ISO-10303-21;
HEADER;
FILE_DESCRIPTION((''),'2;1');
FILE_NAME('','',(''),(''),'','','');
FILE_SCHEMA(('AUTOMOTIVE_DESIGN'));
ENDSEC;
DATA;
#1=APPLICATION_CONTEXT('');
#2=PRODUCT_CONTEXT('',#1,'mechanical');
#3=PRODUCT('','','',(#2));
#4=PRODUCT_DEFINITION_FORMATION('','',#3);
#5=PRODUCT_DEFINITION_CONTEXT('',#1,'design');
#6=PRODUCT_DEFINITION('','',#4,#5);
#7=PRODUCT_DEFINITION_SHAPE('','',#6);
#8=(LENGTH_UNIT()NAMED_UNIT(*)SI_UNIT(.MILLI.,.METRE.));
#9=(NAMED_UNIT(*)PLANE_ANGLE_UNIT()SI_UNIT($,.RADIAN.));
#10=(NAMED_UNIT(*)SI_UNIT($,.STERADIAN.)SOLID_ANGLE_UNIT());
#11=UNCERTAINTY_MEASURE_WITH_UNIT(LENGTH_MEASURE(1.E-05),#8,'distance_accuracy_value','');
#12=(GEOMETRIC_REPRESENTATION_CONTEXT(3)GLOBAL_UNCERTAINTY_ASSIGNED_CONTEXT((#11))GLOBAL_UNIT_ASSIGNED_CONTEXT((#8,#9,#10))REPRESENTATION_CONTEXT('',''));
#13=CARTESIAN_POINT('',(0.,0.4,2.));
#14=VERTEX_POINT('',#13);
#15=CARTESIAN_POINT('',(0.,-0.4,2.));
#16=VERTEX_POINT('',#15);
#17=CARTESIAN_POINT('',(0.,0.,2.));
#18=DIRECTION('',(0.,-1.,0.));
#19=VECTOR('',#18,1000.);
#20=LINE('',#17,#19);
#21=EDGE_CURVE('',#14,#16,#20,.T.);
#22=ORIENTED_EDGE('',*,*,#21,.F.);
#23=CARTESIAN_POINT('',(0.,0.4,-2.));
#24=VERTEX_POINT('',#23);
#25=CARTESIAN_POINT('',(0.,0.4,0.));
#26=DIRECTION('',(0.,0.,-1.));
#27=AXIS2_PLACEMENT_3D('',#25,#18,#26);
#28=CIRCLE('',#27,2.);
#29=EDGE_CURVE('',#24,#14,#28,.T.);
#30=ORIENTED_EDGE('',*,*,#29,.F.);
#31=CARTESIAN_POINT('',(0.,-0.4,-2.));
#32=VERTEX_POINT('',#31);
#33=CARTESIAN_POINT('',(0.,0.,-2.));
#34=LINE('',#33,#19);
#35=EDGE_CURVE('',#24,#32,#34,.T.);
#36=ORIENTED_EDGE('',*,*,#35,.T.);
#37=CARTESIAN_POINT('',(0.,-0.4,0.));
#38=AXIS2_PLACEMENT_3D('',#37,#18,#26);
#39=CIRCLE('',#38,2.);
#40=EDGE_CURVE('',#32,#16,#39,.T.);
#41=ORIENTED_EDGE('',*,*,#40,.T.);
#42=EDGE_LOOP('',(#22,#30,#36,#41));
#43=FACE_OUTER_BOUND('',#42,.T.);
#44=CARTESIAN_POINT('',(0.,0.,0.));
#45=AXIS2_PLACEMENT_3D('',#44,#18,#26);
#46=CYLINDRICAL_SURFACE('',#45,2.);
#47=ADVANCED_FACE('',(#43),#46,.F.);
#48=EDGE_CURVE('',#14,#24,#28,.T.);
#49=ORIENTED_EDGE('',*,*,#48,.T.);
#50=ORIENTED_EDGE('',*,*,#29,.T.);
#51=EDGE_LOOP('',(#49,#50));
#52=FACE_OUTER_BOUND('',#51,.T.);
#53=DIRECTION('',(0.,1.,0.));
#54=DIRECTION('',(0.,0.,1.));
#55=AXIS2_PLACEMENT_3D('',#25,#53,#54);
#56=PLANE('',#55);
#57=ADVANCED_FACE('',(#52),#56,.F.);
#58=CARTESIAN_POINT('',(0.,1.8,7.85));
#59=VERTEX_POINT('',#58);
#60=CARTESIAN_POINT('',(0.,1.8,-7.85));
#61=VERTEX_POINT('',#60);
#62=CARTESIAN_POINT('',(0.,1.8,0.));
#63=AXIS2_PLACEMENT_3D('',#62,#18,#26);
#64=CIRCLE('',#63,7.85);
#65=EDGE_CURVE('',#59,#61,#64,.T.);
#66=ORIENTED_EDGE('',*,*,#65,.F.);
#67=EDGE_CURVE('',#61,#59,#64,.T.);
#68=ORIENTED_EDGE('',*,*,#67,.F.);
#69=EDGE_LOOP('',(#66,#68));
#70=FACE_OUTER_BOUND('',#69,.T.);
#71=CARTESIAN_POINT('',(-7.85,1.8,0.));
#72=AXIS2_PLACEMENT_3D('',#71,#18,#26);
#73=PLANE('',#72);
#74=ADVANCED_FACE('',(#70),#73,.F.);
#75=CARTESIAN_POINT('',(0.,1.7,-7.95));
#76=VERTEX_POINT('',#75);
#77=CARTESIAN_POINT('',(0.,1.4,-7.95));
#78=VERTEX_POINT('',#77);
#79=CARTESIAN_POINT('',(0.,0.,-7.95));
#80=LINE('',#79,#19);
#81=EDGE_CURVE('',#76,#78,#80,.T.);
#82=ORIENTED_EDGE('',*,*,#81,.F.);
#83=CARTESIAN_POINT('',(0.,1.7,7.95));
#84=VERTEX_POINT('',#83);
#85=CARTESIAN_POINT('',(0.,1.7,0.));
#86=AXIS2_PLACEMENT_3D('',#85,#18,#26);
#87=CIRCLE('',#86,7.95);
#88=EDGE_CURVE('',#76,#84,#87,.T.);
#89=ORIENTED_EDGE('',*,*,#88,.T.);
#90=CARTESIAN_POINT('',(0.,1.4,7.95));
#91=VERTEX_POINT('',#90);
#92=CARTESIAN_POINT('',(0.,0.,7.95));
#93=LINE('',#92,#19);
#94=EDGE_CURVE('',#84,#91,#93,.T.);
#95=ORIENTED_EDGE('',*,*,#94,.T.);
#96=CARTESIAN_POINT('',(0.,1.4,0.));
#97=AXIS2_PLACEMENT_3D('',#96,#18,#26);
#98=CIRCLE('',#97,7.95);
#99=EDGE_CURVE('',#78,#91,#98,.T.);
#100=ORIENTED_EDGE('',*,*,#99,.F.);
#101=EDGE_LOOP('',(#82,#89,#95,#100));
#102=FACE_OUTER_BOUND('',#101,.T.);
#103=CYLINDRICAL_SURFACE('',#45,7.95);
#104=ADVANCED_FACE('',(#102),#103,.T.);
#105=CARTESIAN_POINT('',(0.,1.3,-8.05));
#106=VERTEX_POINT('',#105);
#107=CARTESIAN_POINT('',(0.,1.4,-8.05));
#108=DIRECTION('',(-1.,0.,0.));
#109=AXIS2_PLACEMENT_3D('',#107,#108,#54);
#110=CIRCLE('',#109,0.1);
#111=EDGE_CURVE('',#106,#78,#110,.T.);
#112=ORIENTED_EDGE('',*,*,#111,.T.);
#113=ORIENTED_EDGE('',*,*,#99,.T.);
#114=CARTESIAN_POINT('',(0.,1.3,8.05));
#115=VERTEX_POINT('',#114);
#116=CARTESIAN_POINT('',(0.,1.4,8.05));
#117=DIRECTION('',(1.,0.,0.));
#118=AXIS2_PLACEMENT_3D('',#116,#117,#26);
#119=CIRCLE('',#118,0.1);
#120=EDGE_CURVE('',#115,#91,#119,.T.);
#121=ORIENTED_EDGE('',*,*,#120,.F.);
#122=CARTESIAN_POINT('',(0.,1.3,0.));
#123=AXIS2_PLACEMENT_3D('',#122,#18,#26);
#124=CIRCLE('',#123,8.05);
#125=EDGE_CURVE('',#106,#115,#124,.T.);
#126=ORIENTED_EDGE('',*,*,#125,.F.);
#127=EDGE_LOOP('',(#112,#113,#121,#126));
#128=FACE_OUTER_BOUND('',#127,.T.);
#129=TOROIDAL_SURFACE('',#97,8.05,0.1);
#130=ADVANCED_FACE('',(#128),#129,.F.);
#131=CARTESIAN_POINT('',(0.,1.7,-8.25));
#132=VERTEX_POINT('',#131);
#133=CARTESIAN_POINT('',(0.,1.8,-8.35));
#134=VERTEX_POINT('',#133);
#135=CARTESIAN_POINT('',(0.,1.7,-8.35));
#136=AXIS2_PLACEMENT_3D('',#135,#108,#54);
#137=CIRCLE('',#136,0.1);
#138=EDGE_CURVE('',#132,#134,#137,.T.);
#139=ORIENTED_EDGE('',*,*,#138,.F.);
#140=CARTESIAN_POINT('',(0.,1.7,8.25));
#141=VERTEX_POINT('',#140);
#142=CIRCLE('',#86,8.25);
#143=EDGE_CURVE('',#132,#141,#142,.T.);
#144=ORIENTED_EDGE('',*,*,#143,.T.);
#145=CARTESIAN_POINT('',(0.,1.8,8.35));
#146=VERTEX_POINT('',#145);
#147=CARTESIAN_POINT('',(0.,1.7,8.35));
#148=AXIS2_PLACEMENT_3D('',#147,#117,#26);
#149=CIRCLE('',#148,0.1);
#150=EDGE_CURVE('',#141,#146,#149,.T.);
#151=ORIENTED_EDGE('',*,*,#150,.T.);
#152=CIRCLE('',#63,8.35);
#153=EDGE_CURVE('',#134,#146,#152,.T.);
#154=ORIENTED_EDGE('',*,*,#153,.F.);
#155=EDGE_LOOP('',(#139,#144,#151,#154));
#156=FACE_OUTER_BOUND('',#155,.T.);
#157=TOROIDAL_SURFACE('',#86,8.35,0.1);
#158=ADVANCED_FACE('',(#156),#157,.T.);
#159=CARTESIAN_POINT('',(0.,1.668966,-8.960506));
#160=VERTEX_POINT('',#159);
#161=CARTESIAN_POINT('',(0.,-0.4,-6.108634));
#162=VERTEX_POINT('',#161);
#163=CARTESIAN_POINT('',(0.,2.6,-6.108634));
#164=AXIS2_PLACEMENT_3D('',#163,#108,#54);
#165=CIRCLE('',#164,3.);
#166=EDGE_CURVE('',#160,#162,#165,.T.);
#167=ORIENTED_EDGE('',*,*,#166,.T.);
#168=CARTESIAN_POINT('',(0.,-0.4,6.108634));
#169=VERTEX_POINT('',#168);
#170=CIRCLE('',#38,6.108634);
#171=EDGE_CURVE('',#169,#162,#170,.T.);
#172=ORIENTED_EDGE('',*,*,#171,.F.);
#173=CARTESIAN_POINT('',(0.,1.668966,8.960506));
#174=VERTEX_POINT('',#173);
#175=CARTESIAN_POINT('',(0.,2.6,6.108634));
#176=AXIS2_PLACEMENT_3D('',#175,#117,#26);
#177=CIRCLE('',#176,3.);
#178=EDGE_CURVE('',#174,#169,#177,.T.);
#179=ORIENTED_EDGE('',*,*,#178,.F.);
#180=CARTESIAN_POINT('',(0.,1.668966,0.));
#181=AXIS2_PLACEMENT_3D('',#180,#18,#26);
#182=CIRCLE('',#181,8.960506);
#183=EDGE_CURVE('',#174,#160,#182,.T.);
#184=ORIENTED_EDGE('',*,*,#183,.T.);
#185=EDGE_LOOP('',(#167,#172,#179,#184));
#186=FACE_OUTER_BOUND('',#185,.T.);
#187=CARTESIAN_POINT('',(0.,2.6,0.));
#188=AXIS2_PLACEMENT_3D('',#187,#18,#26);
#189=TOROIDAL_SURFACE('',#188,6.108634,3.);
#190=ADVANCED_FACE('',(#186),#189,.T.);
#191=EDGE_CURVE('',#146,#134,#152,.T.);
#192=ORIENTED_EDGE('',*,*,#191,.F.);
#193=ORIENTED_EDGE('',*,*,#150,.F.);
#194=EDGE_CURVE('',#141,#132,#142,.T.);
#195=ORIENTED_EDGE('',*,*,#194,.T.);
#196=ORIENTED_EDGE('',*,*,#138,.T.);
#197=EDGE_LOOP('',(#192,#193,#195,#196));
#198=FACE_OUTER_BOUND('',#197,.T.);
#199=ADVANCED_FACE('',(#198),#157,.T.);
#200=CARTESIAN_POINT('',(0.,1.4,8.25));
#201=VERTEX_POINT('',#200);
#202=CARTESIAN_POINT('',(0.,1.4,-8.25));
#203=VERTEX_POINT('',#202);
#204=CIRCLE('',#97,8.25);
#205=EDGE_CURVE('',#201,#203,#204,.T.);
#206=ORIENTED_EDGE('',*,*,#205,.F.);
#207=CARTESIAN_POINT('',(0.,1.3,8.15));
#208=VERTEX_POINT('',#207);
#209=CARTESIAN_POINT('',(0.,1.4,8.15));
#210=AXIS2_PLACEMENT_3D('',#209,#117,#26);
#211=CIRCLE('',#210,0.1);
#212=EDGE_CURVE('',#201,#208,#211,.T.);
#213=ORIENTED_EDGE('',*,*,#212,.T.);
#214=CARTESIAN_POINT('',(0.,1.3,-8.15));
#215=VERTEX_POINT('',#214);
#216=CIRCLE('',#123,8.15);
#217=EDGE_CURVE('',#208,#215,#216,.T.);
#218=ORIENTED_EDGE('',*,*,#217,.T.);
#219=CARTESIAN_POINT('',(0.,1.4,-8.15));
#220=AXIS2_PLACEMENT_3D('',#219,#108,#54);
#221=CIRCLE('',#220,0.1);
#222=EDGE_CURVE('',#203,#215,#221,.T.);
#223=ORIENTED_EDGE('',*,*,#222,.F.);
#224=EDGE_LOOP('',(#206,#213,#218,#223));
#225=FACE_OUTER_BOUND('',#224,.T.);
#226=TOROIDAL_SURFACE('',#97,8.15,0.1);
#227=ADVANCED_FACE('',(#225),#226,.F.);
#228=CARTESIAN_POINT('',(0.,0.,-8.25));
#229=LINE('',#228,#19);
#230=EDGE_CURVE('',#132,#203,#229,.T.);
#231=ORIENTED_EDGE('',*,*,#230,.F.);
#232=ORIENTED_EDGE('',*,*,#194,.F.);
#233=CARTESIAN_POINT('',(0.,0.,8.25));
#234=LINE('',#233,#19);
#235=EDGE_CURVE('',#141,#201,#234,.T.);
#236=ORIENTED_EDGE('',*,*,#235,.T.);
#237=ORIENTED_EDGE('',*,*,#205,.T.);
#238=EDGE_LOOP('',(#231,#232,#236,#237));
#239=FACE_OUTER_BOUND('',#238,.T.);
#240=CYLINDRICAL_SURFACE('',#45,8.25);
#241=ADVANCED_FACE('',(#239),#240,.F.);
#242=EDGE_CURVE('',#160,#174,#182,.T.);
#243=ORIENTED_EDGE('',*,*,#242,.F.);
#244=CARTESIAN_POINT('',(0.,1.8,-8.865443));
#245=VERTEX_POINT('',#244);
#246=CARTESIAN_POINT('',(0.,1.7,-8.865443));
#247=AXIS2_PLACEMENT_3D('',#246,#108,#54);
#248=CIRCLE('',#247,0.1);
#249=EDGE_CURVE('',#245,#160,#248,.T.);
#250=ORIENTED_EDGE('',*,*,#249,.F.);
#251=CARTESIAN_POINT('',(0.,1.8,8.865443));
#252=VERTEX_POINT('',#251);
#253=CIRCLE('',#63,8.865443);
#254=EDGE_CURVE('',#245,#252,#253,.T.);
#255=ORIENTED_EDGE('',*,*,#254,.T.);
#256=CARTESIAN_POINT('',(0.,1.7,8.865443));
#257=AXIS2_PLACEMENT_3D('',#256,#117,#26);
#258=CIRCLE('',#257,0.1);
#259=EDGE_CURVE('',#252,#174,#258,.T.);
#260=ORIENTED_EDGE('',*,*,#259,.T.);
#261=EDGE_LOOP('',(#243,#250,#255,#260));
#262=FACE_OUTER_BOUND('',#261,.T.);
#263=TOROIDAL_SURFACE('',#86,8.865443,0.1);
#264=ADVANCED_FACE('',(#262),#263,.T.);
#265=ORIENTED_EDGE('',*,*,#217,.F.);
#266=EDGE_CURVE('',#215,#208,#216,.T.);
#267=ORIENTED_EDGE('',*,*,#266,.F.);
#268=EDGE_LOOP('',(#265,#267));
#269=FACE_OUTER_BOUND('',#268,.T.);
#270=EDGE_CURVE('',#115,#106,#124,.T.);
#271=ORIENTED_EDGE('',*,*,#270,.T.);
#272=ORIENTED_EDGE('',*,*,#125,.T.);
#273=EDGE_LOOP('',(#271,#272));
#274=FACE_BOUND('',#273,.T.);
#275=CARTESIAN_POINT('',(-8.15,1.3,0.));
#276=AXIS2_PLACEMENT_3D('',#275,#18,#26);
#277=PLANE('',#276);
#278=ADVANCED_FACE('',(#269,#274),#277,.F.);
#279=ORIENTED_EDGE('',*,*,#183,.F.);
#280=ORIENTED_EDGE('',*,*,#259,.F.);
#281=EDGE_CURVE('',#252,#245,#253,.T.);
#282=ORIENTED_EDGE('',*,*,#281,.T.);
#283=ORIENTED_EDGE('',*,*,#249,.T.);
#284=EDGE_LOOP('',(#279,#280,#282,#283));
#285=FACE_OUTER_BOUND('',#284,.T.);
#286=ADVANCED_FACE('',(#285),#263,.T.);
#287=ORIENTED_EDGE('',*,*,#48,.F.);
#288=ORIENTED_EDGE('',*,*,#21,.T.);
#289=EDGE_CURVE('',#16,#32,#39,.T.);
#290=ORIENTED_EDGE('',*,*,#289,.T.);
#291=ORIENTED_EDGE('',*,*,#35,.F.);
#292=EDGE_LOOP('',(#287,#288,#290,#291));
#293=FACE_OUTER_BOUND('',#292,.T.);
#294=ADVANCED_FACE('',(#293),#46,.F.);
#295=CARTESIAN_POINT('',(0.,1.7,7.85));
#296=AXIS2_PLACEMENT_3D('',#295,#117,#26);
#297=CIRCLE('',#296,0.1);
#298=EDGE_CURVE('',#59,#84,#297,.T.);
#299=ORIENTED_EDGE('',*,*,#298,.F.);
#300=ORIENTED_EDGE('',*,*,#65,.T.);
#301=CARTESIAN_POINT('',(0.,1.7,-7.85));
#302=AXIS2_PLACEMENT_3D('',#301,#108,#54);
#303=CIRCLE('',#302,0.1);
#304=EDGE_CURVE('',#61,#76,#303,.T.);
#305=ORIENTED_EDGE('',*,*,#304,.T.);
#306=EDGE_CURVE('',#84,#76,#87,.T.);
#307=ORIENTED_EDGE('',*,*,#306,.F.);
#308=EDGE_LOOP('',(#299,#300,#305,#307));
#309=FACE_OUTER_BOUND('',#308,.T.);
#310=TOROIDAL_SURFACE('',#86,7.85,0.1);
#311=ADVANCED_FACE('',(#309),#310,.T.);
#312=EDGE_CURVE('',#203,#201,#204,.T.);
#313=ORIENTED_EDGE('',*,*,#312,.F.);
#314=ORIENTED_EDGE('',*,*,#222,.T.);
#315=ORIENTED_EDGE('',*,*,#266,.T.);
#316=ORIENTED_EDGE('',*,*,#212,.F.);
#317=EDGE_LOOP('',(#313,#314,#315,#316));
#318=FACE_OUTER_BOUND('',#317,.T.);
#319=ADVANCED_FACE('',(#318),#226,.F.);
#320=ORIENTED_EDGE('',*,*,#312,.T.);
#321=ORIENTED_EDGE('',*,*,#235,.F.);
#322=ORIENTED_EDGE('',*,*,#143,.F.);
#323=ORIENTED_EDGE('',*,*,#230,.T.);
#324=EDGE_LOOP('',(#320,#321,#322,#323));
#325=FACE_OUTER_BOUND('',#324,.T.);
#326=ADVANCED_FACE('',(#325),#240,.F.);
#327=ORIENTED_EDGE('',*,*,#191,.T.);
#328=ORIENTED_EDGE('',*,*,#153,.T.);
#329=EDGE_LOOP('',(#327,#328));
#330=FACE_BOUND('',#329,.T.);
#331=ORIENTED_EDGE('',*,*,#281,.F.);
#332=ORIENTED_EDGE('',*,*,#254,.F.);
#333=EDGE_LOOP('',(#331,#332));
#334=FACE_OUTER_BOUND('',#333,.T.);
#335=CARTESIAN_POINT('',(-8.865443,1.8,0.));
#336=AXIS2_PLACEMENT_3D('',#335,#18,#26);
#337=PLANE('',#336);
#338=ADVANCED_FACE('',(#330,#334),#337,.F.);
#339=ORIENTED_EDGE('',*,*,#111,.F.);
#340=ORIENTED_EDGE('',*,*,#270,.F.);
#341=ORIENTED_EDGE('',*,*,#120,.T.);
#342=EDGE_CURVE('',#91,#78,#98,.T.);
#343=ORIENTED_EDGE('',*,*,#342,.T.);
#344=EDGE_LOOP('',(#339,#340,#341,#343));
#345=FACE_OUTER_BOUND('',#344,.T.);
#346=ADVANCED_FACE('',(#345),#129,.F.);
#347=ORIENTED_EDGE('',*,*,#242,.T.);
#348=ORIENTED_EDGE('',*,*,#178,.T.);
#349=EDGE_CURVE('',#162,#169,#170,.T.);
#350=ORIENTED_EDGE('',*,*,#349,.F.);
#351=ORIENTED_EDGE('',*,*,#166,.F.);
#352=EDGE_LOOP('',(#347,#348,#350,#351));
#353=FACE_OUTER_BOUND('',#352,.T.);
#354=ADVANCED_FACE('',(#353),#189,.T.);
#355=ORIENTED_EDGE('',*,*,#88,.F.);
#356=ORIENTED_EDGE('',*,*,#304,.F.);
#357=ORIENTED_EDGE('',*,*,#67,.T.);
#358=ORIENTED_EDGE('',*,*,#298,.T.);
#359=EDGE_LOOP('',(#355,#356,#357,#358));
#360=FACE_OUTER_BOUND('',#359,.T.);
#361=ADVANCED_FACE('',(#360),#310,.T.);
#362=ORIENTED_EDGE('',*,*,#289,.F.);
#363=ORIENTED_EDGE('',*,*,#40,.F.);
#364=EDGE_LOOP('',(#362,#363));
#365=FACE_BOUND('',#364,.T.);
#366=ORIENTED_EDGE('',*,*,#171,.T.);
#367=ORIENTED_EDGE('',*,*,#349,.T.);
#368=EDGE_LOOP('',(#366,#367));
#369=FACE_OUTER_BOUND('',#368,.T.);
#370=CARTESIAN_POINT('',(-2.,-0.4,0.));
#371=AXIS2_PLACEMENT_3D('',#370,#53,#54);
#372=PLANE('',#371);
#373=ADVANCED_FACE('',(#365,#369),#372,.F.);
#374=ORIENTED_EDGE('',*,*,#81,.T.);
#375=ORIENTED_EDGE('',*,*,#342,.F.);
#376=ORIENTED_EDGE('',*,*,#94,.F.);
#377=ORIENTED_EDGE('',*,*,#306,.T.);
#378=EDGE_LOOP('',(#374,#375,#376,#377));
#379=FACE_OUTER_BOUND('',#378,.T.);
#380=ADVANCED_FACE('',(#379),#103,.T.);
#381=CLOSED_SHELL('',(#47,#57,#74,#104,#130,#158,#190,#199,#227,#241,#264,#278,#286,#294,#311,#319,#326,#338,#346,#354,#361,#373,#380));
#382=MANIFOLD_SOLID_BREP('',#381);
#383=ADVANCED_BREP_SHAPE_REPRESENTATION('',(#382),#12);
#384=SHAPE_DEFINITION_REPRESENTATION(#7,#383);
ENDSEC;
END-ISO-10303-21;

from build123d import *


with BuildPart() as part:
    # Sketch 1 → Revolve1 (revolve)
    with BuildSketch(Plane.XY, mode=Mode.PRIVATE) as revolve1_sk:
        with BuildLine():
            Line((-2, -0.4), (-6.108633541, -0.4))
            ThreePointArc((-6.108633541, -0.4), (-7.8702942, 0.17171836), (-8.960505697, 1.668965517))
            ThreePointArc((-8.960505697, 1.668965517), (-8.946386013, 1.758722022), (-8.865443291, 1.8))
            Line((-8.865443291, 1.8), (-8.35, 1.8))
            ThreePointArc((-8.35, 1.8), (-8.279289322, 1.770710678), (-8.25, 1.7))
            Line((-8.25, 1.7), (-8.25, 1.4))
            ThreePointArc((-8.25, 1.4), (-8.220710678, 1.329289322), (-8.15, 1.3))
            Line((-8.15, 1.3), (-8.05, 1.3))
            ThreePointArc((-8.05, 1.3), (-7.979289322, 1.329289322), (-7.95, 1.4))
            Line((-7.95, 1.4), (-7.95, 1.7))
            ThreePointArc((-7.95, 1.7), (-7.920710678, 1.770710678), (-7.85, 1.8))
            Line((-7.85, 1.8), (0, 1.8))
            Line((0, 1.8), (0, 0.4))
            Line((0, 0.4), (-2, 0.4))
            Line((-2, 0.4), (-2, -0.4))
        make_face()
    revolve(revolve1_sk.sketch.rotate(Axis((0, 0, 0), (0, 1, 0)), 270), axis=Axis((0, 0, 0), (0, 1, 0)))


solid = part.part
